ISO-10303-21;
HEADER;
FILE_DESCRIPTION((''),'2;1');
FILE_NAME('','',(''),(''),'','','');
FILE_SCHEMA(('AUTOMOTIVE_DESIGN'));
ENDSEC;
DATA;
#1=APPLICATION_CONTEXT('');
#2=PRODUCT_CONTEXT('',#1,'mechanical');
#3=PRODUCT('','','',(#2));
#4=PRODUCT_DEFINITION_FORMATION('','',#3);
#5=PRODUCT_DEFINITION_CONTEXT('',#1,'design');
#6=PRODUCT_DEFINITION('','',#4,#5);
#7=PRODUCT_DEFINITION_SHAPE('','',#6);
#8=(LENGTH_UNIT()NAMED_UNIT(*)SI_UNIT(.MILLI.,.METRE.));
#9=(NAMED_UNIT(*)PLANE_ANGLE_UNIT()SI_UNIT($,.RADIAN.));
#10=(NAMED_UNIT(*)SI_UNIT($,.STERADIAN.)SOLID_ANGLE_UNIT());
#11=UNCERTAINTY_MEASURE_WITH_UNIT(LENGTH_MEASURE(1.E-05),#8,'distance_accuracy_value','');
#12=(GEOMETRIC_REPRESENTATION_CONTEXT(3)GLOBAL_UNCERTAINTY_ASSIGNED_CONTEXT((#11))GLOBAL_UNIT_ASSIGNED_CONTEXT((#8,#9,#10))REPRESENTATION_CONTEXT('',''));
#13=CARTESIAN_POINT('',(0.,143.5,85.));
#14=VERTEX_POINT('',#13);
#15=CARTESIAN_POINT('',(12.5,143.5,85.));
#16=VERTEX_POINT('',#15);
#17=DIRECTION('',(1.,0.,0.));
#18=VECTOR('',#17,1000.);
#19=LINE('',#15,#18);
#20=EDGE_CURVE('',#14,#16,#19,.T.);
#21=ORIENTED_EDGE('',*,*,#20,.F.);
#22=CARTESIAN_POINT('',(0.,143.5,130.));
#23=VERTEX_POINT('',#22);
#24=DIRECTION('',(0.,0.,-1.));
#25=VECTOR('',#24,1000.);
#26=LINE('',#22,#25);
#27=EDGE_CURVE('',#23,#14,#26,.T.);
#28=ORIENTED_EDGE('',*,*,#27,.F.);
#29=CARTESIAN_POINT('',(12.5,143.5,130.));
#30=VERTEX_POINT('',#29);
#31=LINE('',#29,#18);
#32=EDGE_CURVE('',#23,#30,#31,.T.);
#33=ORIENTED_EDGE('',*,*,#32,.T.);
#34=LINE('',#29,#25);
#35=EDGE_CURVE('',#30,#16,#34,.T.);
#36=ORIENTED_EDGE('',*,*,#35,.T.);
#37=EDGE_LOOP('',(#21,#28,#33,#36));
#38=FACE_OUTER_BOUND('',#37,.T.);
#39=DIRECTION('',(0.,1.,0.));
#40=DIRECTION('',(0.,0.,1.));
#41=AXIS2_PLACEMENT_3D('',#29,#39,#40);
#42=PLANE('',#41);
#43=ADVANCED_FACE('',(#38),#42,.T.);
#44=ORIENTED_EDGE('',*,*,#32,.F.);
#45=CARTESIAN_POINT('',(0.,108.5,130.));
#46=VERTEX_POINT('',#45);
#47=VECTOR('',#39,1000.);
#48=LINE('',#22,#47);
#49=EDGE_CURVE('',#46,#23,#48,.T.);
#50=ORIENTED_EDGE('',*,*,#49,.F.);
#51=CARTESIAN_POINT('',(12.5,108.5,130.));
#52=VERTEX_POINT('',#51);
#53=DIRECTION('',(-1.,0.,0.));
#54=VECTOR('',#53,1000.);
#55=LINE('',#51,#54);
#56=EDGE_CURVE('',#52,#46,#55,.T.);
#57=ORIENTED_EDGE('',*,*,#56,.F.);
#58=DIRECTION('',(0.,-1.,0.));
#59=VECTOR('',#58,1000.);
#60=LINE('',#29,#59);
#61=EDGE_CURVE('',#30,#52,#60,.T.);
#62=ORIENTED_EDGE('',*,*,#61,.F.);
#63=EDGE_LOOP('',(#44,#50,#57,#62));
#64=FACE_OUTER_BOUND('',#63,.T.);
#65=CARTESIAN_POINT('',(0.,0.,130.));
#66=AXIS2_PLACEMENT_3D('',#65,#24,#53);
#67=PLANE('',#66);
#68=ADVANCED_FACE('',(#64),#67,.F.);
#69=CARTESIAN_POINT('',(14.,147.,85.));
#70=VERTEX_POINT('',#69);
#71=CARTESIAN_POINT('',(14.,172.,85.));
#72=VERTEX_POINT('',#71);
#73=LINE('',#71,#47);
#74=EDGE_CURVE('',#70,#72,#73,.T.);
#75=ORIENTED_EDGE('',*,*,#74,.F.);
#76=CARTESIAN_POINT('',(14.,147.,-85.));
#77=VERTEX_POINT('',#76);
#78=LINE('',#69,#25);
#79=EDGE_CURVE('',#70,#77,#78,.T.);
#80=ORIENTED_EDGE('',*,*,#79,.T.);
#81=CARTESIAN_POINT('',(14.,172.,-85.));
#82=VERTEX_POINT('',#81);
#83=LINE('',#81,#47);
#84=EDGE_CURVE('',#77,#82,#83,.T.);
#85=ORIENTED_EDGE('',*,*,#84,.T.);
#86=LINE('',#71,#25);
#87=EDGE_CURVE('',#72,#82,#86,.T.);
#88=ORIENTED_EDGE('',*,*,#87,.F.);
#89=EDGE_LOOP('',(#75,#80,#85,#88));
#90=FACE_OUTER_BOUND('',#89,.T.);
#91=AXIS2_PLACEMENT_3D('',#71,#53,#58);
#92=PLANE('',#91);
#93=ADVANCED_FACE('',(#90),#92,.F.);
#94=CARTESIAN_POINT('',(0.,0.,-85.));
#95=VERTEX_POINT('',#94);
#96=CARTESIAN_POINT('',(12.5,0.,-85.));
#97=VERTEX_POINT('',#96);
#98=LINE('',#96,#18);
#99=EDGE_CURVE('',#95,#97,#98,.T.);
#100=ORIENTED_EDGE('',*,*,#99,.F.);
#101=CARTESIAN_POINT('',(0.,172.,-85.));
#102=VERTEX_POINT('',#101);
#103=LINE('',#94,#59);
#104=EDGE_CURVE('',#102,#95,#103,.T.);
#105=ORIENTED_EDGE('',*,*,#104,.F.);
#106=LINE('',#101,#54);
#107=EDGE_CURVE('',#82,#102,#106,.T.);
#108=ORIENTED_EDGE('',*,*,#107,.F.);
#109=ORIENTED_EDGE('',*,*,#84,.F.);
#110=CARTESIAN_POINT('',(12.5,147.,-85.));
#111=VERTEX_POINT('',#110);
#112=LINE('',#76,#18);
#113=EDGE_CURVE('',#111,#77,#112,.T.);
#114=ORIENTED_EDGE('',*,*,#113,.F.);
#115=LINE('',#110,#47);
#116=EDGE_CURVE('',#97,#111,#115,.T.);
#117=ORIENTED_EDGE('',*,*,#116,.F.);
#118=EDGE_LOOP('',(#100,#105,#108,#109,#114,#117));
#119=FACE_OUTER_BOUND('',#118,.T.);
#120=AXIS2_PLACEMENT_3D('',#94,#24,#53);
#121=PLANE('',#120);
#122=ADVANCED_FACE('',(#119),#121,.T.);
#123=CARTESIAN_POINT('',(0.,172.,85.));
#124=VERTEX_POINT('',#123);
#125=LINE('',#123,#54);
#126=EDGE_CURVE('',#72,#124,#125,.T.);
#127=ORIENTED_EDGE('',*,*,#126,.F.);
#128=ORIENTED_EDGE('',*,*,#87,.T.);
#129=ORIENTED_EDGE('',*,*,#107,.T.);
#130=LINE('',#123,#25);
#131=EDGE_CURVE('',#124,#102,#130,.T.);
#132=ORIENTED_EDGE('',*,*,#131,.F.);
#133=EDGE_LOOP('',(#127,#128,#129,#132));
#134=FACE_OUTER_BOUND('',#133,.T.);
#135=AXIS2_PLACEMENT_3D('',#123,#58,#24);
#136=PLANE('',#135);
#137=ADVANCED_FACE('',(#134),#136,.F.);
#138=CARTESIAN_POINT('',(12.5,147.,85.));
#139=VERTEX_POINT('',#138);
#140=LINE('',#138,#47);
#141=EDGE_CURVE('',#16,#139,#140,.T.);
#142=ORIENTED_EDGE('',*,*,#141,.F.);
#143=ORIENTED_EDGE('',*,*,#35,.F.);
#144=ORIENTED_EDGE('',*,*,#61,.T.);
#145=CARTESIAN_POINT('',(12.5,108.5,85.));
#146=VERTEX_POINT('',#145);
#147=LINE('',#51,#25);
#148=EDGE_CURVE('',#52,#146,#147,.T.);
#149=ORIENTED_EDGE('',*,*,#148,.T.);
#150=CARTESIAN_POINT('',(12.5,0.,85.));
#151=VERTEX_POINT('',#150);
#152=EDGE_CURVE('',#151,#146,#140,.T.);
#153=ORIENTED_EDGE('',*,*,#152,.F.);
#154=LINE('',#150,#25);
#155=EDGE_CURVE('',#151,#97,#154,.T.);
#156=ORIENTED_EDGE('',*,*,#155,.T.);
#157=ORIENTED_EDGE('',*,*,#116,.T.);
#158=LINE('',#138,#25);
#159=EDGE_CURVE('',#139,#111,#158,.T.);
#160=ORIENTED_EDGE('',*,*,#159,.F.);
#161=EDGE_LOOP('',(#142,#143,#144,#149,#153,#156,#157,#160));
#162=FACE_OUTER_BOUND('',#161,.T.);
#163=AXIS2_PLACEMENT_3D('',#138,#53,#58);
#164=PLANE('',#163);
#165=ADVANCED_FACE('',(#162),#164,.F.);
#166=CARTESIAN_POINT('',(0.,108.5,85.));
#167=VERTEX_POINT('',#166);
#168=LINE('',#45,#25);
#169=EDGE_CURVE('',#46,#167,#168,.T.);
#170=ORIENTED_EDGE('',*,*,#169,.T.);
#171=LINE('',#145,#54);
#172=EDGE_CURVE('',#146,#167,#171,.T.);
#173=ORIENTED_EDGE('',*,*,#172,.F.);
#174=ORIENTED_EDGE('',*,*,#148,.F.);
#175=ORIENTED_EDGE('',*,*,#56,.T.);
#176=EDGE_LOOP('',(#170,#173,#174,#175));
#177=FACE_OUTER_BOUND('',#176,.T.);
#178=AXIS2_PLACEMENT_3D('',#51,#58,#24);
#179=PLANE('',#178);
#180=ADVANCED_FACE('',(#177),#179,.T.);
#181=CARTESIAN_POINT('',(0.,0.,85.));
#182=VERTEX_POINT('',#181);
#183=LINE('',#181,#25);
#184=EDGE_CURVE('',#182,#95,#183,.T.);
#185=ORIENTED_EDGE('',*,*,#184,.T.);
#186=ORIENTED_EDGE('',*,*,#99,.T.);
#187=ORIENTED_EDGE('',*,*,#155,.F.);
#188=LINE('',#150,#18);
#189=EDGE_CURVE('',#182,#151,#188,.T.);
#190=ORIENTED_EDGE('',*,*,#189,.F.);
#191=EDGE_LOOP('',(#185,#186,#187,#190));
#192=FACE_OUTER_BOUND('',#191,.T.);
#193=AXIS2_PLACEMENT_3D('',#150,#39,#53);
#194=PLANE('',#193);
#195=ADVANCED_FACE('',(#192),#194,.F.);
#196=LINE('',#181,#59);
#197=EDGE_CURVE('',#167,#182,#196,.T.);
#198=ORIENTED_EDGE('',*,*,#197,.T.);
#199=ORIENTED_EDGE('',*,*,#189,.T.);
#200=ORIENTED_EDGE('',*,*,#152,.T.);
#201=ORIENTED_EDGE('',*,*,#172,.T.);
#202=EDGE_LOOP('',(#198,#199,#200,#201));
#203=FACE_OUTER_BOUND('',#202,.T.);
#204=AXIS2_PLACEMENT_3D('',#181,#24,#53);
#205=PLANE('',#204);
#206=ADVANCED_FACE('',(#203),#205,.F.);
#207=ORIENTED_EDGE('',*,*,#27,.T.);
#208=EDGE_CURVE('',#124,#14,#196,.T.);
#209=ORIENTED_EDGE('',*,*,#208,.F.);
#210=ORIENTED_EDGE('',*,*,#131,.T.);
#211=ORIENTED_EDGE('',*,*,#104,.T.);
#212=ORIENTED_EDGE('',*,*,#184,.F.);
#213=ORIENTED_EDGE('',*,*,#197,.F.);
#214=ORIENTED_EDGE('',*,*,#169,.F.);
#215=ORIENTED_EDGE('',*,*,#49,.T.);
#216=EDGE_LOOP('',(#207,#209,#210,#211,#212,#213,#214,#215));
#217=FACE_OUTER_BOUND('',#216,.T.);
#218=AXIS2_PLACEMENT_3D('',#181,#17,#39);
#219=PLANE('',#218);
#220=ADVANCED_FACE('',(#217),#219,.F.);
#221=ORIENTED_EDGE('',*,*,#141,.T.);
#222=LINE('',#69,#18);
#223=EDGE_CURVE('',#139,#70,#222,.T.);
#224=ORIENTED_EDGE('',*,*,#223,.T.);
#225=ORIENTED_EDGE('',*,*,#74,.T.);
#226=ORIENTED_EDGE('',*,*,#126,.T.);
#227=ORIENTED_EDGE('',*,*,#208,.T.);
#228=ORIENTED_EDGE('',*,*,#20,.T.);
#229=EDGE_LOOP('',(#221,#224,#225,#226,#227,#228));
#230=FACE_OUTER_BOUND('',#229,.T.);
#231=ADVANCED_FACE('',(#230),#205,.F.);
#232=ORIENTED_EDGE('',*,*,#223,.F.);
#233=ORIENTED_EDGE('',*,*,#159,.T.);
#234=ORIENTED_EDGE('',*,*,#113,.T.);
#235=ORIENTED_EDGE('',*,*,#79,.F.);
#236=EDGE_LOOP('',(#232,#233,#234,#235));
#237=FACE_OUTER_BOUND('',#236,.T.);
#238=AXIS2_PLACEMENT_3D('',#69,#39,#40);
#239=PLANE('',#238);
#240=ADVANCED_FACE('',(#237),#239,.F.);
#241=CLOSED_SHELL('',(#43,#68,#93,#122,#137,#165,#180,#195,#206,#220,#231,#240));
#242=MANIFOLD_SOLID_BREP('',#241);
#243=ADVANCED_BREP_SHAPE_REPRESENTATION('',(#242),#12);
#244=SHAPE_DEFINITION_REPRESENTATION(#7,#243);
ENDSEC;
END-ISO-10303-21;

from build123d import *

# Parameters (mm, degrees)
EXTRUDE_1_DEPTH = 85
SKETCH_4_W      = 12.5
SKETCH_4_H      = 35
EXTRUDE_2_DEPTH = 45


with BuildPart() as part:
    # 草图1 → 凸台-拉伸1 (new, symmetric)
    with BuildSketch(Plane.XY):
        Polygon((0, 0), (0, 172), (14, 172), (14, 147), (12.5, 147), (12.5, 0), align=None)
    extrude(amount=EXTRUDE_1_DEPTH, both=True)

    # 草图4 → 凸台-拉伸2 (add)
    with BuildSketch(Plane(origin=(0, 0, 85), x_dir=(-1, 0, 0), z_dir=(0, 0, -1))):
        with Locations((-6.25, 126)):
            Rectangle(SKETCH_4_W, SKETCH_4_H)
    extrude(amount=-EXTRUDE_2_DEPTH)


solid = part.part
